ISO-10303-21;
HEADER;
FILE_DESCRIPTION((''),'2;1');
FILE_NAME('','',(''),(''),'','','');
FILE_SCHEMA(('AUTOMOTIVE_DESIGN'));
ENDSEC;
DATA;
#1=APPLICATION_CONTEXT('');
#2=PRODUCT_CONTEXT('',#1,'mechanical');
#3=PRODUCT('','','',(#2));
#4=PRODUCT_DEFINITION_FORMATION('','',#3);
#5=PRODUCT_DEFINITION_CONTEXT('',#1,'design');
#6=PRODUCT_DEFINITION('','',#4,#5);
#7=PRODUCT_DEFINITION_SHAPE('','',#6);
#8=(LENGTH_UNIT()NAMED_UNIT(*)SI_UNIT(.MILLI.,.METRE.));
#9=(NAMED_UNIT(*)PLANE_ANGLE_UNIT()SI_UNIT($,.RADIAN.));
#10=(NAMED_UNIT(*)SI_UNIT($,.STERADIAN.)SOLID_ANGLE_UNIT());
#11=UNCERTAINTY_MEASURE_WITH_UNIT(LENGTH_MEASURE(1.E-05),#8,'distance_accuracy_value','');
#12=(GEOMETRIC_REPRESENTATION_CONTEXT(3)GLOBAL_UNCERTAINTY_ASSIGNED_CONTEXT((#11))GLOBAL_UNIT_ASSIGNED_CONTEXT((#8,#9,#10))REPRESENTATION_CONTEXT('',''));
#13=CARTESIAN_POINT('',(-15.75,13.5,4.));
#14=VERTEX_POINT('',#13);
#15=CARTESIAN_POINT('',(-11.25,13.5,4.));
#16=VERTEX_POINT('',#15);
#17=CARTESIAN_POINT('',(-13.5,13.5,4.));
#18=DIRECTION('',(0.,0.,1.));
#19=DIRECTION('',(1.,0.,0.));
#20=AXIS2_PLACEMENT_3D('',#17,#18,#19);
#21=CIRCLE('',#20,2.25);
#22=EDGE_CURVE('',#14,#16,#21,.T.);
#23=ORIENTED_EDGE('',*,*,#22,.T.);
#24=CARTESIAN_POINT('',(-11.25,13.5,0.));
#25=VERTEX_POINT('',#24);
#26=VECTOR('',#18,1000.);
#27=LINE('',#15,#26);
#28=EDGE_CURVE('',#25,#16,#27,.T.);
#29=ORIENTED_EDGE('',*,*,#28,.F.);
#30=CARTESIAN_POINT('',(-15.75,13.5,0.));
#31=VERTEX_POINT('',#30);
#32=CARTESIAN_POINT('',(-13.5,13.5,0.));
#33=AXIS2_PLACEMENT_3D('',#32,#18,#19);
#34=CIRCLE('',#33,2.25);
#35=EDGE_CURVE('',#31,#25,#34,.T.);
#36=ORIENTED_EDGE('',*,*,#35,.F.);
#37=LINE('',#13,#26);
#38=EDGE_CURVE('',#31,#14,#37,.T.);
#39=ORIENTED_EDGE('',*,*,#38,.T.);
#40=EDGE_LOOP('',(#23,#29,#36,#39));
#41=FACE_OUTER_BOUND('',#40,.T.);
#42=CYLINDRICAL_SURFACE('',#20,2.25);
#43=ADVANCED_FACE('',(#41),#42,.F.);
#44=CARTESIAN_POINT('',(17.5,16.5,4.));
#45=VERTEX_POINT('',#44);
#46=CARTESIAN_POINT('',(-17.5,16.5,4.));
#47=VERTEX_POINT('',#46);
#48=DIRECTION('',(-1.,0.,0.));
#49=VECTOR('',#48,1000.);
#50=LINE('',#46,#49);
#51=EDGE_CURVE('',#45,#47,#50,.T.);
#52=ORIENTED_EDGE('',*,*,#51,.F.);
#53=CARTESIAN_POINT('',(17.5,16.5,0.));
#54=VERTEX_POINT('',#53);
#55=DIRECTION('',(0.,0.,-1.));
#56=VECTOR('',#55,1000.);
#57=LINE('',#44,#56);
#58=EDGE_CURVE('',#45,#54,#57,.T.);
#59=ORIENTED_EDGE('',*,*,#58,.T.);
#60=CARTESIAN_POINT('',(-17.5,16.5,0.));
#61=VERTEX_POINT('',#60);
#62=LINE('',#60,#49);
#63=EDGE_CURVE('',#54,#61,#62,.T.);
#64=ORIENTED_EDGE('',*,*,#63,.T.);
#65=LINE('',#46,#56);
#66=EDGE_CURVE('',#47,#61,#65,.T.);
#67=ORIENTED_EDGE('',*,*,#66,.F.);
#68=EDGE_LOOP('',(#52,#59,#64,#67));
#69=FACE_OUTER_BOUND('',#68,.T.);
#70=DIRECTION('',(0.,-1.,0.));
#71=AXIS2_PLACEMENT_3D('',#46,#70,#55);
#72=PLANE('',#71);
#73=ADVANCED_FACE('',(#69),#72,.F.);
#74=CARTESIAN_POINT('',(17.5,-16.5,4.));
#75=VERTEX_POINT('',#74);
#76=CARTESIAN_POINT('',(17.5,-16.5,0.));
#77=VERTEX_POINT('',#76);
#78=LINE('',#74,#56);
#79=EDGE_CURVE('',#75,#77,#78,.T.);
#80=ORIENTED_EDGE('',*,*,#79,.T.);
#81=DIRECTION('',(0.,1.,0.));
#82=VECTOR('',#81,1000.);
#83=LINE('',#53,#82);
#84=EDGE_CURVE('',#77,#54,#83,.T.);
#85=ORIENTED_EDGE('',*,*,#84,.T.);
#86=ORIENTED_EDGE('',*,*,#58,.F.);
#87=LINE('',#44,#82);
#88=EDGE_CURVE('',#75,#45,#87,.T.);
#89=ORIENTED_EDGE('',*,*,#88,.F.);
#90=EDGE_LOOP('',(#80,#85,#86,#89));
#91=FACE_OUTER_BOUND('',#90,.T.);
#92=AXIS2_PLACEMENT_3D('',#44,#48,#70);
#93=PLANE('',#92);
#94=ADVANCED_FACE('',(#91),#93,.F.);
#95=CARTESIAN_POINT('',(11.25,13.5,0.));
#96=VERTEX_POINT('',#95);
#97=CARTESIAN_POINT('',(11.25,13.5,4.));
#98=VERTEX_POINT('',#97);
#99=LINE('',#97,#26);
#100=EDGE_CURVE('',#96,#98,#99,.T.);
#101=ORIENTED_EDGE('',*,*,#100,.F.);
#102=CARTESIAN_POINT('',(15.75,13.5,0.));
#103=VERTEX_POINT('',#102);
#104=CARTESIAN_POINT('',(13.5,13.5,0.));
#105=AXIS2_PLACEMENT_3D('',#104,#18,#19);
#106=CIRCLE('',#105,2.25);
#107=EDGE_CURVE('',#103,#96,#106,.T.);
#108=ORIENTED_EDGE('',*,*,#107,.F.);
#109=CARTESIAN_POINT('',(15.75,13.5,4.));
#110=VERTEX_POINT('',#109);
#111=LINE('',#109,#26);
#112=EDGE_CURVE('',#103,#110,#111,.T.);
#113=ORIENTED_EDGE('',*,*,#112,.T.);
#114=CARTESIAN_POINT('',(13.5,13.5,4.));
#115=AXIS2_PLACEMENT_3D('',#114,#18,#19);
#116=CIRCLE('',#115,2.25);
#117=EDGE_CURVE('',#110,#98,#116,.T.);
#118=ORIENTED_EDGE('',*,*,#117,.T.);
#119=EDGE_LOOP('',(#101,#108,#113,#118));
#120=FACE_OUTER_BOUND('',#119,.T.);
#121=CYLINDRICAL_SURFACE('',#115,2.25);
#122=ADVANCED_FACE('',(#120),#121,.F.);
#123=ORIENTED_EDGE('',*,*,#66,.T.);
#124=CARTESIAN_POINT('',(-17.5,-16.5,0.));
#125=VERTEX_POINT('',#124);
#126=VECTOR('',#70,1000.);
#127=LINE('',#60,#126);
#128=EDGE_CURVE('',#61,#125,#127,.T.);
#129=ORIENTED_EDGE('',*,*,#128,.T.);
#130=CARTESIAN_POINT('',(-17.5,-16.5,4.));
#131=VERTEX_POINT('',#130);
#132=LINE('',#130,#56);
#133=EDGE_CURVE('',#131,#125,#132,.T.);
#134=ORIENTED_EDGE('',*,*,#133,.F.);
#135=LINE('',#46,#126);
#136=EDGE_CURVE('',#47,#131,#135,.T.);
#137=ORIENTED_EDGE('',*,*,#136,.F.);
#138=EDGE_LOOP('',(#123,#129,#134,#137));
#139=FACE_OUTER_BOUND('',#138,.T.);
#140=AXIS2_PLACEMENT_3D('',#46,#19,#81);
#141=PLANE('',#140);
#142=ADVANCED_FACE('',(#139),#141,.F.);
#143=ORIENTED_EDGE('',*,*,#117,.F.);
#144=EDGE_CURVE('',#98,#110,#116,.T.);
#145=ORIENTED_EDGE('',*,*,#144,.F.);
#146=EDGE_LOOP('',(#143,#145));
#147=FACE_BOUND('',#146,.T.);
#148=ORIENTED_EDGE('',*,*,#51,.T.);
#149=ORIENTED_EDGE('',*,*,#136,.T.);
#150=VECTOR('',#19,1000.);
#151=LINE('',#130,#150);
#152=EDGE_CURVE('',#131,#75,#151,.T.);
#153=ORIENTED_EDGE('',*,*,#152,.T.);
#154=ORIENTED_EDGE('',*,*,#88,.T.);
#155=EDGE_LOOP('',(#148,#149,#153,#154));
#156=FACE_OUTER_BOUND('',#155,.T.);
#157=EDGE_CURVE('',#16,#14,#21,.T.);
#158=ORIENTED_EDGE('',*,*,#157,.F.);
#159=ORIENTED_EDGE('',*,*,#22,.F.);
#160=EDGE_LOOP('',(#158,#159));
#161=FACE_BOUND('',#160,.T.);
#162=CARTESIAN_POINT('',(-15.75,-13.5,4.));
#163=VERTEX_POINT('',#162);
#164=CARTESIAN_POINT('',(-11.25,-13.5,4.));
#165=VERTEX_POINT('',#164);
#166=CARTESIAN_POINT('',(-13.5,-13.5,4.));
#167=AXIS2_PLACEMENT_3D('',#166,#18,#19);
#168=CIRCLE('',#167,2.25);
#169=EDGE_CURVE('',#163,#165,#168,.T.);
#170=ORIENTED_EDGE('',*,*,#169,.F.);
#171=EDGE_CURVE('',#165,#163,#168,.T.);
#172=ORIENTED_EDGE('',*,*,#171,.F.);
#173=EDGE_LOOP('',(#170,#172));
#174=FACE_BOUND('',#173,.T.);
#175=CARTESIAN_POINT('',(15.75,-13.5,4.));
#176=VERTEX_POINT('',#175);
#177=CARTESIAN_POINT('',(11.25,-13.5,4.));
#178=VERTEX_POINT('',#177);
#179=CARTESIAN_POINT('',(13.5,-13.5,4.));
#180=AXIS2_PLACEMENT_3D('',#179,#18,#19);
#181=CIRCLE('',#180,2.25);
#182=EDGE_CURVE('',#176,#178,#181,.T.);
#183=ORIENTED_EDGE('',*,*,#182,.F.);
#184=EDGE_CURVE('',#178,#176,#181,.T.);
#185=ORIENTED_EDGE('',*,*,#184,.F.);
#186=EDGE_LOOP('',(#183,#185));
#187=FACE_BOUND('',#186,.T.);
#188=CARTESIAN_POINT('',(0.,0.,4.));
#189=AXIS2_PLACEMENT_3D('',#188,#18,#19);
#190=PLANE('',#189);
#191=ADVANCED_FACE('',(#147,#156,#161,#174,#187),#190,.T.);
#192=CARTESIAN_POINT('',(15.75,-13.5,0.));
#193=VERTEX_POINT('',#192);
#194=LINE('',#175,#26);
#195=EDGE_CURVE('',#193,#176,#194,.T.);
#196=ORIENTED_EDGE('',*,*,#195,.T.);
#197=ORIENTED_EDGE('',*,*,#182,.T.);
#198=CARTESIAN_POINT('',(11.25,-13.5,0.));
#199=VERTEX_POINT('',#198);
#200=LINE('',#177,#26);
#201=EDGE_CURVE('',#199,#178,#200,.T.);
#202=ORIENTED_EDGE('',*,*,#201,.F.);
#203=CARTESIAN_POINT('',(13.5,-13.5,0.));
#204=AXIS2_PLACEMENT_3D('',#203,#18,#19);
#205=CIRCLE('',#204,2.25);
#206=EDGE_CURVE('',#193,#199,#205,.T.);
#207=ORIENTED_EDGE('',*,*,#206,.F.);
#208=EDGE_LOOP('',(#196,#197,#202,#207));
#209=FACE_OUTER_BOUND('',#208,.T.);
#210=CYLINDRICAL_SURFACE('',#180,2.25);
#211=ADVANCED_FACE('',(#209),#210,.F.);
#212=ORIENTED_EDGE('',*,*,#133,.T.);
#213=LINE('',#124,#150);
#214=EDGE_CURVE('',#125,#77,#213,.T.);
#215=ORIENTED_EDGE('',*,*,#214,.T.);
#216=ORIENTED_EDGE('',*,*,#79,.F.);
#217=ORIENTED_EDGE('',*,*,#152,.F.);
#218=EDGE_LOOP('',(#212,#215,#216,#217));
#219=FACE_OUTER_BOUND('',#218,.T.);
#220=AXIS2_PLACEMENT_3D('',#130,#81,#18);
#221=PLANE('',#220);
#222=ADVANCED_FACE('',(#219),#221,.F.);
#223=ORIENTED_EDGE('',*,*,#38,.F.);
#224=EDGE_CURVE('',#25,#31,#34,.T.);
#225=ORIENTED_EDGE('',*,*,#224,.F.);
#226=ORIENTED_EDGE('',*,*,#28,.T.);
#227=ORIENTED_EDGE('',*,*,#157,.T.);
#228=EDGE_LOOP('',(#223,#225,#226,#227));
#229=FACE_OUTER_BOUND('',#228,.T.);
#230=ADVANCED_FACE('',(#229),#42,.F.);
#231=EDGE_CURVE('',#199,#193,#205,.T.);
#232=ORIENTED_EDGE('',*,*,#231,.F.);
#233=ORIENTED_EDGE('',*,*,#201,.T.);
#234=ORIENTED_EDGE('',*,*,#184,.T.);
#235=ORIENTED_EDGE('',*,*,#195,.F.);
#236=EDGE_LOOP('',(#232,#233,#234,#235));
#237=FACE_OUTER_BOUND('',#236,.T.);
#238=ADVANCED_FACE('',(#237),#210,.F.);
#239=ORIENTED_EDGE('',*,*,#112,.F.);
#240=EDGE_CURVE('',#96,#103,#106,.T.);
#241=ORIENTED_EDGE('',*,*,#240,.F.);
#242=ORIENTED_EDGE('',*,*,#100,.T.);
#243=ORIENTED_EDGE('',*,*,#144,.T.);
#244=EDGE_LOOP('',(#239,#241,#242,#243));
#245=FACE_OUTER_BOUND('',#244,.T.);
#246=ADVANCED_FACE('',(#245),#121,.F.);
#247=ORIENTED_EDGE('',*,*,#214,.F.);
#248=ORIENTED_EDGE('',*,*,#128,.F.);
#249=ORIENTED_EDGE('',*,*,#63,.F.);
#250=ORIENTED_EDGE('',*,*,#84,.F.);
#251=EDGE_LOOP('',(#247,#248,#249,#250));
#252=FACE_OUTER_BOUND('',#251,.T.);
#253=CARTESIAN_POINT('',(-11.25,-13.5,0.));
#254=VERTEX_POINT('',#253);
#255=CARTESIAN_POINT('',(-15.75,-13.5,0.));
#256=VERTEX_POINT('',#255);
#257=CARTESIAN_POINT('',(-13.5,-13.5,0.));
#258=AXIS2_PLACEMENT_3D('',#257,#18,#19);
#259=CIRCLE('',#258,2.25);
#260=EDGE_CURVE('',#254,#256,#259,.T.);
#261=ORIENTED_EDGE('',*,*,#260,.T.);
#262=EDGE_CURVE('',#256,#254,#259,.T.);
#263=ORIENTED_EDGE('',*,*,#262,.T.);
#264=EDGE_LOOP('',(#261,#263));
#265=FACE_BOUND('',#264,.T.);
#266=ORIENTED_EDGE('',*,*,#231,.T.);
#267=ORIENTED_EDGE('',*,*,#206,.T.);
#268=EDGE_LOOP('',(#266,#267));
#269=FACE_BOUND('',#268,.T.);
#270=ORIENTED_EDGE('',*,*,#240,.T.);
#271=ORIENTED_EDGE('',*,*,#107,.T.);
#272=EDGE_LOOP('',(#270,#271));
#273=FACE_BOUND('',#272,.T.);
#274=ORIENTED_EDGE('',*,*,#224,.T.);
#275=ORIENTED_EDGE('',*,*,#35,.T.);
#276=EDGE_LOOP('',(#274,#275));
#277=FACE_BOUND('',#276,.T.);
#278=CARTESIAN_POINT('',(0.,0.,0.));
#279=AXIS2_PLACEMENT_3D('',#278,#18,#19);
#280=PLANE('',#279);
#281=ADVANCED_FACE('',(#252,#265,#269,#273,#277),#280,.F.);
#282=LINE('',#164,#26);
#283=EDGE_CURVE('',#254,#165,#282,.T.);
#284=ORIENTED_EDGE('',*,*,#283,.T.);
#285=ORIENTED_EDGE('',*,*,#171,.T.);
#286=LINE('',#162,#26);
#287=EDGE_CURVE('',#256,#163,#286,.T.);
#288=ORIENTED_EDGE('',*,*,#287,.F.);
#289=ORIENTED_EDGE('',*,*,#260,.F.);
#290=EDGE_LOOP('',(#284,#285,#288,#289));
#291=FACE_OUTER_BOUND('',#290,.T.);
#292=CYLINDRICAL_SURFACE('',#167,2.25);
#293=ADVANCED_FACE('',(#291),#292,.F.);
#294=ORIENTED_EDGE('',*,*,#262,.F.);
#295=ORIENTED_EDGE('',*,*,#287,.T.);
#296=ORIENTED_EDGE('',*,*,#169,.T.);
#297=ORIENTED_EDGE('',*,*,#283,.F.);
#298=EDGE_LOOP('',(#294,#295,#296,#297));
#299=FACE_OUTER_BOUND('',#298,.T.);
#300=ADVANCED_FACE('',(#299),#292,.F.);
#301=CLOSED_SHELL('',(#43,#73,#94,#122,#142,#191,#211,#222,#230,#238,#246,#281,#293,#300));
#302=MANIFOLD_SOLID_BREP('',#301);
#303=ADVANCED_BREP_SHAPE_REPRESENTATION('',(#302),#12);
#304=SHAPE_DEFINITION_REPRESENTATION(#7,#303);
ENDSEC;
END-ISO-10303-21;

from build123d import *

# Parameters (mm, degrees)
SKETCH1_W                = 35
SKETCH1_H                = 33
BOSS_EXTRUDE1_DEPTH      = 4
M4_CLEARANCE_HOLE1_D     = 4.5
M4_CLEARANCE_HOLE1_DEPTH = 15
M4_CLEARANCE_HOLE1_TIP   = 1.351936393


with BuildPart() as part:
    # Sketch1 → Boss-Extrude1 (new body)
    with BuildSketch(Plane.XY):
        Rectangle(SKETCH1_W, SKETCH1_H)
    extrude(amount=BOSS_EXTRUDE1_DEPTH)

    # M4 Clearance Hole1
    with Locations(Plane.XY.offset(4)):
        with Locations((13.5, 13.5), (-13.5, 13.5), (-13.5, -13.5), (13.5, -13.5)):
            Hole(M4_CLEARANCE_HOLE1_D / 2, depth=M4_CLEARANCE_HOLE1_DEPTH)
            with Locations((0, 0, -(M4_CLEARANCE_HOLE1_DEPTH + M4_CLEARANCE_HOLE1_TIP / 2))):  # 118° drill point
                Cone(0, M4_CLEARANCE_HOLE1_D / 2, M4_CLEARANCE_HOLE1_TIP, mode=Mode.SUBTRACT)


solid = part.part
